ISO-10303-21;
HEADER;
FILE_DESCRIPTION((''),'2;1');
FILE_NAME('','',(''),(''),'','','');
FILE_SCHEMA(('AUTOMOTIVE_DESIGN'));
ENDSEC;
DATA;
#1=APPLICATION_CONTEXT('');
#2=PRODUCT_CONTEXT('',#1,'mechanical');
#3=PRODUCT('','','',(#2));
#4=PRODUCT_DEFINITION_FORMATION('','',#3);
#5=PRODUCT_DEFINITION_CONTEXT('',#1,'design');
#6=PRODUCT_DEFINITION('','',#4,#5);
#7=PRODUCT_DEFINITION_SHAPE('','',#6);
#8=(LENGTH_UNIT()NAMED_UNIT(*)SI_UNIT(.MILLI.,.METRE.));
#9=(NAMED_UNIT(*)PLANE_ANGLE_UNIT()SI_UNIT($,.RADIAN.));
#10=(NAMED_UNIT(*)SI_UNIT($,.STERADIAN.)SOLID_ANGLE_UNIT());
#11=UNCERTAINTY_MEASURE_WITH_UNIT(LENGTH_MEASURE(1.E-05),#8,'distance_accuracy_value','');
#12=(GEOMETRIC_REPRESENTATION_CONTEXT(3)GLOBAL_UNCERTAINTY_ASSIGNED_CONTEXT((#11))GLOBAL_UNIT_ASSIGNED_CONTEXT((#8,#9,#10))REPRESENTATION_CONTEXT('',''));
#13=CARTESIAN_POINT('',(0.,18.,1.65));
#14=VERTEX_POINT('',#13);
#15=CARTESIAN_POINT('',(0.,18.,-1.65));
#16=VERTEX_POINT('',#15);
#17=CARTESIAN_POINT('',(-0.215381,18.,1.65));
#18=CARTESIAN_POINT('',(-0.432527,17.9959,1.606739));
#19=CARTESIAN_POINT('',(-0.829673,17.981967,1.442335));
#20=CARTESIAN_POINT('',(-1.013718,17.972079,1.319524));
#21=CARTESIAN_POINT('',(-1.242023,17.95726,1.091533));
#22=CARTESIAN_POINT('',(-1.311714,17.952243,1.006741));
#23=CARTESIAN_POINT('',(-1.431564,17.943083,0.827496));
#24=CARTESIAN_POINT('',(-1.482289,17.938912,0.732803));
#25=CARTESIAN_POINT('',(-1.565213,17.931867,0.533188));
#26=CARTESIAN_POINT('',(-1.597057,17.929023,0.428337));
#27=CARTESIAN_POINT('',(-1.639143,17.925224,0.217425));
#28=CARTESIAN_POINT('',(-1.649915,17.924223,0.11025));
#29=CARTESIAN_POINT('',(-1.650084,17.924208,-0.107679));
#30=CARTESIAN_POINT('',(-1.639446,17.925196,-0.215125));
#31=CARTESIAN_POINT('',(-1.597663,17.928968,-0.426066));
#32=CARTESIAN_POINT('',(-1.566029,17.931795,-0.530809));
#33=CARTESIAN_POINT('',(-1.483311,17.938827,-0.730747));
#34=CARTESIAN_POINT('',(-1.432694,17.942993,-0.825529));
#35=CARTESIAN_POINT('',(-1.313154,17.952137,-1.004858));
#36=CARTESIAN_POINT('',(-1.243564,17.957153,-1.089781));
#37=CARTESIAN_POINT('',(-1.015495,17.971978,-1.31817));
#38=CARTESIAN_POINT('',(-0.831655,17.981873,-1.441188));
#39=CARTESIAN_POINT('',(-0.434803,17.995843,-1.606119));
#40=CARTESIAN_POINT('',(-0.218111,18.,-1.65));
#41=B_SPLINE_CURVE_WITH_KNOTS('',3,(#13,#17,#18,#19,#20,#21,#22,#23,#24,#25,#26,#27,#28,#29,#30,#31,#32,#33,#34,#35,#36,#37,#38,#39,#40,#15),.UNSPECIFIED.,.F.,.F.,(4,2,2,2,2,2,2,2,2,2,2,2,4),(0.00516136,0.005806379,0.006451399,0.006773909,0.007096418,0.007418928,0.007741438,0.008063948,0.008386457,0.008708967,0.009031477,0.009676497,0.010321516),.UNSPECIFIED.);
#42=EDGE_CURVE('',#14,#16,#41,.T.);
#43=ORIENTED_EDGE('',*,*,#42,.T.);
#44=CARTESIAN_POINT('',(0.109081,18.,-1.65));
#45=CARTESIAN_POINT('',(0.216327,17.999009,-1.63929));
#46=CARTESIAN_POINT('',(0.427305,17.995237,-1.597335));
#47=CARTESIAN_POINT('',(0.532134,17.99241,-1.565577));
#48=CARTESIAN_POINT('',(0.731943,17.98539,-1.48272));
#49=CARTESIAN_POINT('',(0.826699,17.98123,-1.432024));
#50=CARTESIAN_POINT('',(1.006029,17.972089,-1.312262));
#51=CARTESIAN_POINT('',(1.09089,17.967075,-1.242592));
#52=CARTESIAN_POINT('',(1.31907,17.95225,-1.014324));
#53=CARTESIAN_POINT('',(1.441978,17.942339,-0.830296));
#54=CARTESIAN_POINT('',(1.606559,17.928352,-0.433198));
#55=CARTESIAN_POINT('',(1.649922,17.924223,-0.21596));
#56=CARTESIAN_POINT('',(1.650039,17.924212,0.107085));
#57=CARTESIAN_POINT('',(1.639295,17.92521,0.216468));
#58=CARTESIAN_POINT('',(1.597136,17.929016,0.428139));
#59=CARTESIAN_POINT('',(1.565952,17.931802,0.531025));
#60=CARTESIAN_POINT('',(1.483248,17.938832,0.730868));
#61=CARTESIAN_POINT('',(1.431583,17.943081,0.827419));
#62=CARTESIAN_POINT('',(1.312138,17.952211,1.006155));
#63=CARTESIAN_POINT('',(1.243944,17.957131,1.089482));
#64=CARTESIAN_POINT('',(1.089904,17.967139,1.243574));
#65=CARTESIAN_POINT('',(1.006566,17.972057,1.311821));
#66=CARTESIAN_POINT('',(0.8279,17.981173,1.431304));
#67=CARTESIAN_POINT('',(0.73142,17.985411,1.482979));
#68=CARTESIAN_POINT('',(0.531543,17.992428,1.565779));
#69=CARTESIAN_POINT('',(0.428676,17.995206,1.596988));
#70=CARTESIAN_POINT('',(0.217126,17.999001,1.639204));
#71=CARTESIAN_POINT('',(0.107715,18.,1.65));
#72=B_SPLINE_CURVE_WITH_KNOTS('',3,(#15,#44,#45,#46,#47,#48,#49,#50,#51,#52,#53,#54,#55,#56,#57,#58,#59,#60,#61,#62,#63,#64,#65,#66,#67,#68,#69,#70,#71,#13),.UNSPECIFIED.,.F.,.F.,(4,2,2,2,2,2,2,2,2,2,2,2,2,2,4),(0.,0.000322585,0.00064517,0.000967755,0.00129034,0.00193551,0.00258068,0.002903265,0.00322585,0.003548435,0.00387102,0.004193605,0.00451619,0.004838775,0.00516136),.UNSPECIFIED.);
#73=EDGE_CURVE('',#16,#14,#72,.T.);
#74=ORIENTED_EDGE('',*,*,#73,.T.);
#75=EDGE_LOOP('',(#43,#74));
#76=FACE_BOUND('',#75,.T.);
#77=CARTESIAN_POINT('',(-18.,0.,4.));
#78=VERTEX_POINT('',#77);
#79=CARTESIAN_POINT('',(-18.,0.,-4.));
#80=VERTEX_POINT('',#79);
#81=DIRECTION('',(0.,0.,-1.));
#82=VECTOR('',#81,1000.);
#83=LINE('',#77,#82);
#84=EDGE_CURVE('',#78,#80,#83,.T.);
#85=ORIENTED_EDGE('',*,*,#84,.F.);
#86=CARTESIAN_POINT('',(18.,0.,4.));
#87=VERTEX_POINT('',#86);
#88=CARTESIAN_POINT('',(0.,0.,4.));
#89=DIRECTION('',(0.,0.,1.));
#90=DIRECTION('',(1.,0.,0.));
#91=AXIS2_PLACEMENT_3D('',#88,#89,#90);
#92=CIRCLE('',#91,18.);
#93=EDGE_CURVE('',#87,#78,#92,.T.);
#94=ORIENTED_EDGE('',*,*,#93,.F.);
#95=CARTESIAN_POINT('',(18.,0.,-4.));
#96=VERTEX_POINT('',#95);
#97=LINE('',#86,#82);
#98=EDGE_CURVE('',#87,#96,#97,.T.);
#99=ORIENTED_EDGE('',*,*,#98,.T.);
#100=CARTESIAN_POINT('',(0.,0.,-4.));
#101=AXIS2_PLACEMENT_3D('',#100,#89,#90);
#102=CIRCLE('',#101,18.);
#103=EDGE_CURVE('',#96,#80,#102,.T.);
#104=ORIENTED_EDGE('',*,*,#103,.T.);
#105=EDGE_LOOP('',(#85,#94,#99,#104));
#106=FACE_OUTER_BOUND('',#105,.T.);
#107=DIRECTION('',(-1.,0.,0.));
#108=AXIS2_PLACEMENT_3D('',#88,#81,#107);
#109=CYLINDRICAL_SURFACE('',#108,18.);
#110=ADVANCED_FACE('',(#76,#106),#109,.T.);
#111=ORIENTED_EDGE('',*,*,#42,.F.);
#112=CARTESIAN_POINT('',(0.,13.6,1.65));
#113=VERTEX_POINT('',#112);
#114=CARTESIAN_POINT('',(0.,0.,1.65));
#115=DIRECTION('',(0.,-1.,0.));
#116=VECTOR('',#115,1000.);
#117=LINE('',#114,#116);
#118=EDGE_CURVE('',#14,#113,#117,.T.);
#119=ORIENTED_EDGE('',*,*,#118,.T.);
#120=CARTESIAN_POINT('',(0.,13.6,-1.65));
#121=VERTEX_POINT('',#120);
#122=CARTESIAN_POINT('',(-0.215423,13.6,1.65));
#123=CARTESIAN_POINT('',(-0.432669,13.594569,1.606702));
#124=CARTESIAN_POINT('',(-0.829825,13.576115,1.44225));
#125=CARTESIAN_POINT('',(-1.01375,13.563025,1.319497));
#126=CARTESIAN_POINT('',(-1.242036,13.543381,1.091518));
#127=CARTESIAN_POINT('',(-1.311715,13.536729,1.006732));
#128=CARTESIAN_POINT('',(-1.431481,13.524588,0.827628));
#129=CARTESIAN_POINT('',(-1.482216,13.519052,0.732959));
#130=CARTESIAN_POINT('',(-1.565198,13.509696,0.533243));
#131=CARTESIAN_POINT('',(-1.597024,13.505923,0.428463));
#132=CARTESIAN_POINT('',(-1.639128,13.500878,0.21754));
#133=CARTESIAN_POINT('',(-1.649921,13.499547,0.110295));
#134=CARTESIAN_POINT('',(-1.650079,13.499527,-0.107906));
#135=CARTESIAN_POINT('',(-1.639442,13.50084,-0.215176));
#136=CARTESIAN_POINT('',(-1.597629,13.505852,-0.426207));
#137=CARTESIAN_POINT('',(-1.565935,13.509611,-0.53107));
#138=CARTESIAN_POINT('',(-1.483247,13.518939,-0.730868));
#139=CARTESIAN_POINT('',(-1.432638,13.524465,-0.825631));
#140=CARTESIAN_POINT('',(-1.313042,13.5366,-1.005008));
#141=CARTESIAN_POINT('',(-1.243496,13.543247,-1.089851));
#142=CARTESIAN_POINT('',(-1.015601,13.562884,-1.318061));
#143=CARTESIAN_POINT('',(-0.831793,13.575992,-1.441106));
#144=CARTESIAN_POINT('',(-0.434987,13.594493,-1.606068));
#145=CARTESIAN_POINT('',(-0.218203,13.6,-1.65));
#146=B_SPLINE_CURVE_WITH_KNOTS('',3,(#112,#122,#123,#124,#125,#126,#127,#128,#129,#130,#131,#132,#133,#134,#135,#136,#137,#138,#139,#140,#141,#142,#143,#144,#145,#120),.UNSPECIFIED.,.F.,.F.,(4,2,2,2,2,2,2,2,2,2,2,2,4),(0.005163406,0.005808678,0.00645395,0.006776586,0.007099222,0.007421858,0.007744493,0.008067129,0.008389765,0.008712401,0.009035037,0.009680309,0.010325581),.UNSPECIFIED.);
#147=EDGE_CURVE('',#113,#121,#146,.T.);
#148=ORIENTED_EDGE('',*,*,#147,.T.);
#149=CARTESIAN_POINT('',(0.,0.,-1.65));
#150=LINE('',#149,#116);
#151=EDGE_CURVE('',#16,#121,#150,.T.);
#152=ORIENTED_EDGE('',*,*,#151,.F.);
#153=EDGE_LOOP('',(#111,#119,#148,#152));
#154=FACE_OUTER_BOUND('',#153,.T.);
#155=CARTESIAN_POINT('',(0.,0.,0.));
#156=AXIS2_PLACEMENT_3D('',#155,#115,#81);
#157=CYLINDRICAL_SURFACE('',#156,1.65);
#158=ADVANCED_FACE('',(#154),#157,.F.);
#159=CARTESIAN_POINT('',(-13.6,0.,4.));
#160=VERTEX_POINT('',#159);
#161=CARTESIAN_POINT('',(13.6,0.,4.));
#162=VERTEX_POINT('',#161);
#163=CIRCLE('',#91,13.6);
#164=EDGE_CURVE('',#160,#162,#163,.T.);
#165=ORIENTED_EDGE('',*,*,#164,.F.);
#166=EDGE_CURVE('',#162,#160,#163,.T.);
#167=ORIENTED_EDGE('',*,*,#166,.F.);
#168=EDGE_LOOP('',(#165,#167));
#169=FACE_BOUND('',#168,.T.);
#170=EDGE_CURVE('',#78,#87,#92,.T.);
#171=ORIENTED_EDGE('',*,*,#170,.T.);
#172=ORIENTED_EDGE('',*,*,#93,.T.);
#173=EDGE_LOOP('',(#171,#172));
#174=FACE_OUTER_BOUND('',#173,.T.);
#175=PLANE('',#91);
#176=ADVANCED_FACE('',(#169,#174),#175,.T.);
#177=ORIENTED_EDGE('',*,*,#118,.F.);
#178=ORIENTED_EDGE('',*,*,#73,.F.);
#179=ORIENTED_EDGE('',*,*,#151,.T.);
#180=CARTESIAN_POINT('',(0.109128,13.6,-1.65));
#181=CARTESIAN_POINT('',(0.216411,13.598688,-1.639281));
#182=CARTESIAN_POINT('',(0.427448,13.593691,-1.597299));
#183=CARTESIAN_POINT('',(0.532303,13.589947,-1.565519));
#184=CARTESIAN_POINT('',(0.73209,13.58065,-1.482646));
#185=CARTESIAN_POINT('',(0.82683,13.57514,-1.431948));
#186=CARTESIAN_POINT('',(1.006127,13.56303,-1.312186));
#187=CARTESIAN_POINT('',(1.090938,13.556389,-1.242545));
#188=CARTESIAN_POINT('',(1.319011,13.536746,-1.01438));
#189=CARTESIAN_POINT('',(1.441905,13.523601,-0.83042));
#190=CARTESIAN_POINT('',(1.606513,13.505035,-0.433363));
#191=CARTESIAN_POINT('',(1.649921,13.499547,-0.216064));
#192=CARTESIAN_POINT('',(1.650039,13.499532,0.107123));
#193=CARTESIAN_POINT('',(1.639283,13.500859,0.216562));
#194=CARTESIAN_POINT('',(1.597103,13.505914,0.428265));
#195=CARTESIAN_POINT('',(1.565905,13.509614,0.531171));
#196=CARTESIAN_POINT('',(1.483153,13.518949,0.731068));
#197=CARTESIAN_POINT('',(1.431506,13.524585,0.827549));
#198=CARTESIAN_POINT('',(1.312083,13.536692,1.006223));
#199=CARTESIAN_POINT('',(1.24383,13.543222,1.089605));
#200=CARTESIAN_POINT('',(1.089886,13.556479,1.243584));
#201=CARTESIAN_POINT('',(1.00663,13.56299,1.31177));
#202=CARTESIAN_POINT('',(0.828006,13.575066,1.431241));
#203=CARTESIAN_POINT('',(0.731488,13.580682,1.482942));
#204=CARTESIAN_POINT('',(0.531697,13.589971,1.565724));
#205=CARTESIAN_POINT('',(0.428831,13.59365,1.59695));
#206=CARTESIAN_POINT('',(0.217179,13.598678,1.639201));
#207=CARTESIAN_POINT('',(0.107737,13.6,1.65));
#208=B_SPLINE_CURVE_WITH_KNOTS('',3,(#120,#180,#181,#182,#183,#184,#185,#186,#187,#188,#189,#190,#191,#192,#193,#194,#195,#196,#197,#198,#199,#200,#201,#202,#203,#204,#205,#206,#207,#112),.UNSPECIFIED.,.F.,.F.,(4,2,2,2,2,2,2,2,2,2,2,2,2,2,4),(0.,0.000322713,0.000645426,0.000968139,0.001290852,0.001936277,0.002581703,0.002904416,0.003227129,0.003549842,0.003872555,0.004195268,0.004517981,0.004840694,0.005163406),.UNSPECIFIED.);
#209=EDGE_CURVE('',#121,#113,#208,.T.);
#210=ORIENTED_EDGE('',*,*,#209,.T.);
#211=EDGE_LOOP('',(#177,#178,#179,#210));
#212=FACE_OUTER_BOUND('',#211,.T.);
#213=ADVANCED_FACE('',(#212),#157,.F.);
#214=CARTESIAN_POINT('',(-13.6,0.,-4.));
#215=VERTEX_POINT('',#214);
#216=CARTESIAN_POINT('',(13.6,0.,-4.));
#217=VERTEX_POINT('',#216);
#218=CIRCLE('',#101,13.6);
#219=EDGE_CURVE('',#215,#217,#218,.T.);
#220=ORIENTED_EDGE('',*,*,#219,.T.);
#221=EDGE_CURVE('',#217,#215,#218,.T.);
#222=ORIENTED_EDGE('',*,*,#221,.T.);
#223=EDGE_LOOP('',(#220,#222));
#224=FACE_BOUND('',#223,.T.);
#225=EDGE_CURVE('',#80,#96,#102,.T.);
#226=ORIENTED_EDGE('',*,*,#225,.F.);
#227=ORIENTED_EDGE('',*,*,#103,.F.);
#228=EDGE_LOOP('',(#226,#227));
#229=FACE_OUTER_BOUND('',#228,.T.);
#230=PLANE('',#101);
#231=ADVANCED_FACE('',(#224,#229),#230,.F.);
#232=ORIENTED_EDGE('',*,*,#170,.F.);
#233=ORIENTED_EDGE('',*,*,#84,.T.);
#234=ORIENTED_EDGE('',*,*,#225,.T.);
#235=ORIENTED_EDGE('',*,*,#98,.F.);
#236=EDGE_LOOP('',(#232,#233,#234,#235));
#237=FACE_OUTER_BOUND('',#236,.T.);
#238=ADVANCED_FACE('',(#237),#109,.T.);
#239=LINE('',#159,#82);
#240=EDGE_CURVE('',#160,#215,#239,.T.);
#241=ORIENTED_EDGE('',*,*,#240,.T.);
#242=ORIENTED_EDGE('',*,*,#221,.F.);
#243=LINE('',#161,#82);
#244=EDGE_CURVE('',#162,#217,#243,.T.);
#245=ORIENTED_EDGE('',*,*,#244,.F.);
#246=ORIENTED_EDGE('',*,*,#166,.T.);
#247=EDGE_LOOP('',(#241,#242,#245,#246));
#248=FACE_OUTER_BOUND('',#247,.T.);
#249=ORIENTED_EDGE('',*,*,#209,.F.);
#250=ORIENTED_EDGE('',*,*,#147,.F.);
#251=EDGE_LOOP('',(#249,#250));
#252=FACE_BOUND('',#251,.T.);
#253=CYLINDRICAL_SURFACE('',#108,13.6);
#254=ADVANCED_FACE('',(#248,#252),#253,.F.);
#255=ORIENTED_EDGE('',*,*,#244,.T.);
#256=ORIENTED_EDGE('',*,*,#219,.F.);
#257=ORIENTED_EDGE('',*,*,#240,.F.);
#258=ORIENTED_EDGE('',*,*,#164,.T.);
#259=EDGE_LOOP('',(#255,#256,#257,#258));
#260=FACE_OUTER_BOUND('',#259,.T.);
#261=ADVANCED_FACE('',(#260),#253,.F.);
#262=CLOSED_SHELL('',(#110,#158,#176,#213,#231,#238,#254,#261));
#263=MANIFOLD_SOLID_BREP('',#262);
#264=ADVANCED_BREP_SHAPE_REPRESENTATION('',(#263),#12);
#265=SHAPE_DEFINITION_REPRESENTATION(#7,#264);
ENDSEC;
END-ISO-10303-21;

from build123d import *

# Parameters (mm, degrees)
SKETCH_1_R      = 18
SKETCH_1_R_2    = 13.6
EXTRUDE_1_DEPTH = 4
SKETCH_8_W      = 1.65
SKETCH_8_H      = 18


with BuildPart() as part:
    # 草图1 → 凸台-拉伸1 (new, symmetric)
    with BuildSketch(Plane.XY):
        Circle(SKETCH_1_R)
        Circle(SKETCH_1_R_2, mode=Mode.SUBTRACT)
    extrude(amount=EXTRUDE_1_DEPTH, both=True)

    # 草图8 → M4 螺纹孔2 (revolve, cut)
    with BuildSketch(Plane(origin=(0, 0, 0), x_dir=(0, 0, -1), z_dir=(1, 0, 0))):
        with Locations((0.825, 9)):
            Rectangle(SKETCH_8_W, SKETCH_8_H)
    revolve(axis=Axis((0, -6.35, 0), (0, 1, 0)), mode=Mode.SUBTRACT)


solid = part.part
